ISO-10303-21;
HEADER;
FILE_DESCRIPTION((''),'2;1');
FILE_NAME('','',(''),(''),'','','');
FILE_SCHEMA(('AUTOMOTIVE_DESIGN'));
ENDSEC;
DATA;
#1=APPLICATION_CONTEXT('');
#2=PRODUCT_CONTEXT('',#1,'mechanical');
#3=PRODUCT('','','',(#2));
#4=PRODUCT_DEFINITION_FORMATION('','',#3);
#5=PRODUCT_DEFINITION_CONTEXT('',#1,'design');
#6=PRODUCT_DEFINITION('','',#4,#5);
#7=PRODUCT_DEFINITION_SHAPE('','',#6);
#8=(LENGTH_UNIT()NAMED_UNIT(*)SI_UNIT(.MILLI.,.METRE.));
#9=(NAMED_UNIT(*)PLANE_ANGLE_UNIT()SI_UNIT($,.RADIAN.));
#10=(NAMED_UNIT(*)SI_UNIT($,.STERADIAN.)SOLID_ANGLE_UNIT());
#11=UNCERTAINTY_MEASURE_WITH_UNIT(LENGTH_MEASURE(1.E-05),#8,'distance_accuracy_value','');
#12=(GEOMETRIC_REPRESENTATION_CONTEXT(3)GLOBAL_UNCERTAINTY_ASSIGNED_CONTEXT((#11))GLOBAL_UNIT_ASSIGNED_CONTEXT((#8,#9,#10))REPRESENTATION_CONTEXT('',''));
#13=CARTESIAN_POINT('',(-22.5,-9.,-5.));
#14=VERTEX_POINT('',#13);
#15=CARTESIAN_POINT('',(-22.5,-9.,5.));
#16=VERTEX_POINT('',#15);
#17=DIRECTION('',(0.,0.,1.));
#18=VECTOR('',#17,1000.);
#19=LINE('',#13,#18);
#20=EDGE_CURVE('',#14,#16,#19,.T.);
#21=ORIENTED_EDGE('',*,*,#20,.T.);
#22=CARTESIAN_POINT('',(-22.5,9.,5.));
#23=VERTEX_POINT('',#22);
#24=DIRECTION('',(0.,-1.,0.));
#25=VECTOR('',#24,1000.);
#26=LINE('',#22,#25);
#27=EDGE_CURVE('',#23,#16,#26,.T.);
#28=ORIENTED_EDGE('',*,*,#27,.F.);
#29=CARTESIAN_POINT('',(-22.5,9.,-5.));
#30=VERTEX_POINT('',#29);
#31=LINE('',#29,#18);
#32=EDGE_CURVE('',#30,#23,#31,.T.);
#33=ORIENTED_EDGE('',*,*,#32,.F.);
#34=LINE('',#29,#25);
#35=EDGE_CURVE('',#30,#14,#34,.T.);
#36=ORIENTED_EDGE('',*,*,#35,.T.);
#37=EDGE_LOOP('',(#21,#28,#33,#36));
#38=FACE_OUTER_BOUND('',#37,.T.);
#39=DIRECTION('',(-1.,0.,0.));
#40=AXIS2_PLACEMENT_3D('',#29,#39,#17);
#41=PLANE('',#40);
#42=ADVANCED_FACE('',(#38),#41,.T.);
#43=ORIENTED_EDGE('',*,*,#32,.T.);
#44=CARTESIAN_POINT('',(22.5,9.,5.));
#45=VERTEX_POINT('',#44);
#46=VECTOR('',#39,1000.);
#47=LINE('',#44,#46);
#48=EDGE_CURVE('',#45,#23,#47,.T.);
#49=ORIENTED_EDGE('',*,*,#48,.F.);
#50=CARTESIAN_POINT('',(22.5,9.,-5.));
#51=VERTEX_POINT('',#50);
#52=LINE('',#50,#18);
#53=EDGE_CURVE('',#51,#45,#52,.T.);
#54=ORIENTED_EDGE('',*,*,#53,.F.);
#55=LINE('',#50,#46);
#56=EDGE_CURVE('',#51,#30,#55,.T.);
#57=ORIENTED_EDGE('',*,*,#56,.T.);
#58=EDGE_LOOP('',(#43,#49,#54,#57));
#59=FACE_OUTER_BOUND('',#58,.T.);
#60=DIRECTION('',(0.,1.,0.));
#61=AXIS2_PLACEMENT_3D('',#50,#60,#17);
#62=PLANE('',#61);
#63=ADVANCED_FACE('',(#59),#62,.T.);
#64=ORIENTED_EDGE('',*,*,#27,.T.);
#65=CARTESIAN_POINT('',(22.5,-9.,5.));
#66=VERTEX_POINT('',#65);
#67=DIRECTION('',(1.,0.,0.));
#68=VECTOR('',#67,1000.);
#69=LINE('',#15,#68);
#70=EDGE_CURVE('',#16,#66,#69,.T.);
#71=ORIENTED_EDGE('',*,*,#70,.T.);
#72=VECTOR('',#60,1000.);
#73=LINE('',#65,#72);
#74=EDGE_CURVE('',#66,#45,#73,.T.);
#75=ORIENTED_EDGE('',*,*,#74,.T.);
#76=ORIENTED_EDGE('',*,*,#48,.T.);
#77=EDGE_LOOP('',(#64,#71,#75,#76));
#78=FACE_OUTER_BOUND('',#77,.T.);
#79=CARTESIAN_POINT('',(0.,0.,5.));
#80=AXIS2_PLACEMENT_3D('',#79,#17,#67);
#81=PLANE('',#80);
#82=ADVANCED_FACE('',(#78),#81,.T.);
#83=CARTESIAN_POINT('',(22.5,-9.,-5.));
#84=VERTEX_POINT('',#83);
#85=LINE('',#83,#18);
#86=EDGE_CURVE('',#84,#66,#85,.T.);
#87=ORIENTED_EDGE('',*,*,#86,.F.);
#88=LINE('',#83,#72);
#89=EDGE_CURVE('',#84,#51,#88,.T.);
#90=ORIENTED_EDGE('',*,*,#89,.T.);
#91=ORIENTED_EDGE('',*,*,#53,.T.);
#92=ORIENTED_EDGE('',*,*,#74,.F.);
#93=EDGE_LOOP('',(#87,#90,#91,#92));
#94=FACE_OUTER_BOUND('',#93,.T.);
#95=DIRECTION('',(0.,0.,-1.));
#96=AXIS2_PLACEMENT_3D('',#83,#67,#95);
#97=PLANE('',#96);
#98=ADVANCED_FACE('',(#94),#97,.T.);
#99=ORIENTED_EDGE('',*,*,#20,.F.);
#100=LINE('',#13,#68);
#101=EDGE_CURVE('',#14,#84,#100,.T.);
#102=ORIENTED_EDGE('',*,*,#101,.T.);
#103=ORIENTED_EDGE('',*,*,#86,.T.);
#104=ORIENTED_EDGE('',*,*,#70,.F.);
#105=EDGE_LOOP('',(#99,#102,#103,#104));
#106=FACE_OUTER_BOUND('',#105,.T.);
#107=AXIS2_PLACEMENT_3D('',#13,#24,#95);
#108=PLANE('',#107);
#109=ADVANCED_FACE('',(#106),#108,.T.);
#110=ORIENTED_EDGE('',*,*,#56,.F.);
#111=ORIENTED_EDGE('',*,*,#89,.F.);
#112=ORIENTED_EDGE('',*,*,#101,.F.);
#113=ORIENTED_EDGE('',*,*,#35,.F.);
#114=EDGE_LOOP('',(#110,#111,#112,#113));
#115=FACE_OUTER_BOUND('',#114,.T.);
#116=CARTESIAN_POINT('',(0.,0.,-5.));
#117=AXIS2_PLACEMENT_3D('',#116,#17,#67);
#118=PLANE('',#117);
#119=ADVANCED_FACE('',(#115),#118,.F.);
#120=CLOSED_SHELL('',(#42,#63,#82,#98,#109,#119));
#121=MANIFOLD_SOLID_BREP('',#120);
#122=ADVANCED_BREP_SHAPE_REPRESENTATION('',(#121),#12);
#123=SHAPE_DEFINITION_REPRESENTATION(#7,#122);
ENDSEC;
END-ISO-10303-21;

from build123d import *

# Parameters (mm, degrees)
SKETCH_1_W      = 45
SKETCH_1_H      = 18
EXTRUDE_1_DEPTH = 5


with BuildPart() as part:
    # 草图1 → 凸台-拉伸1 (new, symmetric)
    with BuildSketch(Plane.XY):
        Rectangle(SKETCH_1_W, SKETCH_1_H)
    extrude(amount=EXTRUDE_1_DEPTH, both=True)


solid = part.part
